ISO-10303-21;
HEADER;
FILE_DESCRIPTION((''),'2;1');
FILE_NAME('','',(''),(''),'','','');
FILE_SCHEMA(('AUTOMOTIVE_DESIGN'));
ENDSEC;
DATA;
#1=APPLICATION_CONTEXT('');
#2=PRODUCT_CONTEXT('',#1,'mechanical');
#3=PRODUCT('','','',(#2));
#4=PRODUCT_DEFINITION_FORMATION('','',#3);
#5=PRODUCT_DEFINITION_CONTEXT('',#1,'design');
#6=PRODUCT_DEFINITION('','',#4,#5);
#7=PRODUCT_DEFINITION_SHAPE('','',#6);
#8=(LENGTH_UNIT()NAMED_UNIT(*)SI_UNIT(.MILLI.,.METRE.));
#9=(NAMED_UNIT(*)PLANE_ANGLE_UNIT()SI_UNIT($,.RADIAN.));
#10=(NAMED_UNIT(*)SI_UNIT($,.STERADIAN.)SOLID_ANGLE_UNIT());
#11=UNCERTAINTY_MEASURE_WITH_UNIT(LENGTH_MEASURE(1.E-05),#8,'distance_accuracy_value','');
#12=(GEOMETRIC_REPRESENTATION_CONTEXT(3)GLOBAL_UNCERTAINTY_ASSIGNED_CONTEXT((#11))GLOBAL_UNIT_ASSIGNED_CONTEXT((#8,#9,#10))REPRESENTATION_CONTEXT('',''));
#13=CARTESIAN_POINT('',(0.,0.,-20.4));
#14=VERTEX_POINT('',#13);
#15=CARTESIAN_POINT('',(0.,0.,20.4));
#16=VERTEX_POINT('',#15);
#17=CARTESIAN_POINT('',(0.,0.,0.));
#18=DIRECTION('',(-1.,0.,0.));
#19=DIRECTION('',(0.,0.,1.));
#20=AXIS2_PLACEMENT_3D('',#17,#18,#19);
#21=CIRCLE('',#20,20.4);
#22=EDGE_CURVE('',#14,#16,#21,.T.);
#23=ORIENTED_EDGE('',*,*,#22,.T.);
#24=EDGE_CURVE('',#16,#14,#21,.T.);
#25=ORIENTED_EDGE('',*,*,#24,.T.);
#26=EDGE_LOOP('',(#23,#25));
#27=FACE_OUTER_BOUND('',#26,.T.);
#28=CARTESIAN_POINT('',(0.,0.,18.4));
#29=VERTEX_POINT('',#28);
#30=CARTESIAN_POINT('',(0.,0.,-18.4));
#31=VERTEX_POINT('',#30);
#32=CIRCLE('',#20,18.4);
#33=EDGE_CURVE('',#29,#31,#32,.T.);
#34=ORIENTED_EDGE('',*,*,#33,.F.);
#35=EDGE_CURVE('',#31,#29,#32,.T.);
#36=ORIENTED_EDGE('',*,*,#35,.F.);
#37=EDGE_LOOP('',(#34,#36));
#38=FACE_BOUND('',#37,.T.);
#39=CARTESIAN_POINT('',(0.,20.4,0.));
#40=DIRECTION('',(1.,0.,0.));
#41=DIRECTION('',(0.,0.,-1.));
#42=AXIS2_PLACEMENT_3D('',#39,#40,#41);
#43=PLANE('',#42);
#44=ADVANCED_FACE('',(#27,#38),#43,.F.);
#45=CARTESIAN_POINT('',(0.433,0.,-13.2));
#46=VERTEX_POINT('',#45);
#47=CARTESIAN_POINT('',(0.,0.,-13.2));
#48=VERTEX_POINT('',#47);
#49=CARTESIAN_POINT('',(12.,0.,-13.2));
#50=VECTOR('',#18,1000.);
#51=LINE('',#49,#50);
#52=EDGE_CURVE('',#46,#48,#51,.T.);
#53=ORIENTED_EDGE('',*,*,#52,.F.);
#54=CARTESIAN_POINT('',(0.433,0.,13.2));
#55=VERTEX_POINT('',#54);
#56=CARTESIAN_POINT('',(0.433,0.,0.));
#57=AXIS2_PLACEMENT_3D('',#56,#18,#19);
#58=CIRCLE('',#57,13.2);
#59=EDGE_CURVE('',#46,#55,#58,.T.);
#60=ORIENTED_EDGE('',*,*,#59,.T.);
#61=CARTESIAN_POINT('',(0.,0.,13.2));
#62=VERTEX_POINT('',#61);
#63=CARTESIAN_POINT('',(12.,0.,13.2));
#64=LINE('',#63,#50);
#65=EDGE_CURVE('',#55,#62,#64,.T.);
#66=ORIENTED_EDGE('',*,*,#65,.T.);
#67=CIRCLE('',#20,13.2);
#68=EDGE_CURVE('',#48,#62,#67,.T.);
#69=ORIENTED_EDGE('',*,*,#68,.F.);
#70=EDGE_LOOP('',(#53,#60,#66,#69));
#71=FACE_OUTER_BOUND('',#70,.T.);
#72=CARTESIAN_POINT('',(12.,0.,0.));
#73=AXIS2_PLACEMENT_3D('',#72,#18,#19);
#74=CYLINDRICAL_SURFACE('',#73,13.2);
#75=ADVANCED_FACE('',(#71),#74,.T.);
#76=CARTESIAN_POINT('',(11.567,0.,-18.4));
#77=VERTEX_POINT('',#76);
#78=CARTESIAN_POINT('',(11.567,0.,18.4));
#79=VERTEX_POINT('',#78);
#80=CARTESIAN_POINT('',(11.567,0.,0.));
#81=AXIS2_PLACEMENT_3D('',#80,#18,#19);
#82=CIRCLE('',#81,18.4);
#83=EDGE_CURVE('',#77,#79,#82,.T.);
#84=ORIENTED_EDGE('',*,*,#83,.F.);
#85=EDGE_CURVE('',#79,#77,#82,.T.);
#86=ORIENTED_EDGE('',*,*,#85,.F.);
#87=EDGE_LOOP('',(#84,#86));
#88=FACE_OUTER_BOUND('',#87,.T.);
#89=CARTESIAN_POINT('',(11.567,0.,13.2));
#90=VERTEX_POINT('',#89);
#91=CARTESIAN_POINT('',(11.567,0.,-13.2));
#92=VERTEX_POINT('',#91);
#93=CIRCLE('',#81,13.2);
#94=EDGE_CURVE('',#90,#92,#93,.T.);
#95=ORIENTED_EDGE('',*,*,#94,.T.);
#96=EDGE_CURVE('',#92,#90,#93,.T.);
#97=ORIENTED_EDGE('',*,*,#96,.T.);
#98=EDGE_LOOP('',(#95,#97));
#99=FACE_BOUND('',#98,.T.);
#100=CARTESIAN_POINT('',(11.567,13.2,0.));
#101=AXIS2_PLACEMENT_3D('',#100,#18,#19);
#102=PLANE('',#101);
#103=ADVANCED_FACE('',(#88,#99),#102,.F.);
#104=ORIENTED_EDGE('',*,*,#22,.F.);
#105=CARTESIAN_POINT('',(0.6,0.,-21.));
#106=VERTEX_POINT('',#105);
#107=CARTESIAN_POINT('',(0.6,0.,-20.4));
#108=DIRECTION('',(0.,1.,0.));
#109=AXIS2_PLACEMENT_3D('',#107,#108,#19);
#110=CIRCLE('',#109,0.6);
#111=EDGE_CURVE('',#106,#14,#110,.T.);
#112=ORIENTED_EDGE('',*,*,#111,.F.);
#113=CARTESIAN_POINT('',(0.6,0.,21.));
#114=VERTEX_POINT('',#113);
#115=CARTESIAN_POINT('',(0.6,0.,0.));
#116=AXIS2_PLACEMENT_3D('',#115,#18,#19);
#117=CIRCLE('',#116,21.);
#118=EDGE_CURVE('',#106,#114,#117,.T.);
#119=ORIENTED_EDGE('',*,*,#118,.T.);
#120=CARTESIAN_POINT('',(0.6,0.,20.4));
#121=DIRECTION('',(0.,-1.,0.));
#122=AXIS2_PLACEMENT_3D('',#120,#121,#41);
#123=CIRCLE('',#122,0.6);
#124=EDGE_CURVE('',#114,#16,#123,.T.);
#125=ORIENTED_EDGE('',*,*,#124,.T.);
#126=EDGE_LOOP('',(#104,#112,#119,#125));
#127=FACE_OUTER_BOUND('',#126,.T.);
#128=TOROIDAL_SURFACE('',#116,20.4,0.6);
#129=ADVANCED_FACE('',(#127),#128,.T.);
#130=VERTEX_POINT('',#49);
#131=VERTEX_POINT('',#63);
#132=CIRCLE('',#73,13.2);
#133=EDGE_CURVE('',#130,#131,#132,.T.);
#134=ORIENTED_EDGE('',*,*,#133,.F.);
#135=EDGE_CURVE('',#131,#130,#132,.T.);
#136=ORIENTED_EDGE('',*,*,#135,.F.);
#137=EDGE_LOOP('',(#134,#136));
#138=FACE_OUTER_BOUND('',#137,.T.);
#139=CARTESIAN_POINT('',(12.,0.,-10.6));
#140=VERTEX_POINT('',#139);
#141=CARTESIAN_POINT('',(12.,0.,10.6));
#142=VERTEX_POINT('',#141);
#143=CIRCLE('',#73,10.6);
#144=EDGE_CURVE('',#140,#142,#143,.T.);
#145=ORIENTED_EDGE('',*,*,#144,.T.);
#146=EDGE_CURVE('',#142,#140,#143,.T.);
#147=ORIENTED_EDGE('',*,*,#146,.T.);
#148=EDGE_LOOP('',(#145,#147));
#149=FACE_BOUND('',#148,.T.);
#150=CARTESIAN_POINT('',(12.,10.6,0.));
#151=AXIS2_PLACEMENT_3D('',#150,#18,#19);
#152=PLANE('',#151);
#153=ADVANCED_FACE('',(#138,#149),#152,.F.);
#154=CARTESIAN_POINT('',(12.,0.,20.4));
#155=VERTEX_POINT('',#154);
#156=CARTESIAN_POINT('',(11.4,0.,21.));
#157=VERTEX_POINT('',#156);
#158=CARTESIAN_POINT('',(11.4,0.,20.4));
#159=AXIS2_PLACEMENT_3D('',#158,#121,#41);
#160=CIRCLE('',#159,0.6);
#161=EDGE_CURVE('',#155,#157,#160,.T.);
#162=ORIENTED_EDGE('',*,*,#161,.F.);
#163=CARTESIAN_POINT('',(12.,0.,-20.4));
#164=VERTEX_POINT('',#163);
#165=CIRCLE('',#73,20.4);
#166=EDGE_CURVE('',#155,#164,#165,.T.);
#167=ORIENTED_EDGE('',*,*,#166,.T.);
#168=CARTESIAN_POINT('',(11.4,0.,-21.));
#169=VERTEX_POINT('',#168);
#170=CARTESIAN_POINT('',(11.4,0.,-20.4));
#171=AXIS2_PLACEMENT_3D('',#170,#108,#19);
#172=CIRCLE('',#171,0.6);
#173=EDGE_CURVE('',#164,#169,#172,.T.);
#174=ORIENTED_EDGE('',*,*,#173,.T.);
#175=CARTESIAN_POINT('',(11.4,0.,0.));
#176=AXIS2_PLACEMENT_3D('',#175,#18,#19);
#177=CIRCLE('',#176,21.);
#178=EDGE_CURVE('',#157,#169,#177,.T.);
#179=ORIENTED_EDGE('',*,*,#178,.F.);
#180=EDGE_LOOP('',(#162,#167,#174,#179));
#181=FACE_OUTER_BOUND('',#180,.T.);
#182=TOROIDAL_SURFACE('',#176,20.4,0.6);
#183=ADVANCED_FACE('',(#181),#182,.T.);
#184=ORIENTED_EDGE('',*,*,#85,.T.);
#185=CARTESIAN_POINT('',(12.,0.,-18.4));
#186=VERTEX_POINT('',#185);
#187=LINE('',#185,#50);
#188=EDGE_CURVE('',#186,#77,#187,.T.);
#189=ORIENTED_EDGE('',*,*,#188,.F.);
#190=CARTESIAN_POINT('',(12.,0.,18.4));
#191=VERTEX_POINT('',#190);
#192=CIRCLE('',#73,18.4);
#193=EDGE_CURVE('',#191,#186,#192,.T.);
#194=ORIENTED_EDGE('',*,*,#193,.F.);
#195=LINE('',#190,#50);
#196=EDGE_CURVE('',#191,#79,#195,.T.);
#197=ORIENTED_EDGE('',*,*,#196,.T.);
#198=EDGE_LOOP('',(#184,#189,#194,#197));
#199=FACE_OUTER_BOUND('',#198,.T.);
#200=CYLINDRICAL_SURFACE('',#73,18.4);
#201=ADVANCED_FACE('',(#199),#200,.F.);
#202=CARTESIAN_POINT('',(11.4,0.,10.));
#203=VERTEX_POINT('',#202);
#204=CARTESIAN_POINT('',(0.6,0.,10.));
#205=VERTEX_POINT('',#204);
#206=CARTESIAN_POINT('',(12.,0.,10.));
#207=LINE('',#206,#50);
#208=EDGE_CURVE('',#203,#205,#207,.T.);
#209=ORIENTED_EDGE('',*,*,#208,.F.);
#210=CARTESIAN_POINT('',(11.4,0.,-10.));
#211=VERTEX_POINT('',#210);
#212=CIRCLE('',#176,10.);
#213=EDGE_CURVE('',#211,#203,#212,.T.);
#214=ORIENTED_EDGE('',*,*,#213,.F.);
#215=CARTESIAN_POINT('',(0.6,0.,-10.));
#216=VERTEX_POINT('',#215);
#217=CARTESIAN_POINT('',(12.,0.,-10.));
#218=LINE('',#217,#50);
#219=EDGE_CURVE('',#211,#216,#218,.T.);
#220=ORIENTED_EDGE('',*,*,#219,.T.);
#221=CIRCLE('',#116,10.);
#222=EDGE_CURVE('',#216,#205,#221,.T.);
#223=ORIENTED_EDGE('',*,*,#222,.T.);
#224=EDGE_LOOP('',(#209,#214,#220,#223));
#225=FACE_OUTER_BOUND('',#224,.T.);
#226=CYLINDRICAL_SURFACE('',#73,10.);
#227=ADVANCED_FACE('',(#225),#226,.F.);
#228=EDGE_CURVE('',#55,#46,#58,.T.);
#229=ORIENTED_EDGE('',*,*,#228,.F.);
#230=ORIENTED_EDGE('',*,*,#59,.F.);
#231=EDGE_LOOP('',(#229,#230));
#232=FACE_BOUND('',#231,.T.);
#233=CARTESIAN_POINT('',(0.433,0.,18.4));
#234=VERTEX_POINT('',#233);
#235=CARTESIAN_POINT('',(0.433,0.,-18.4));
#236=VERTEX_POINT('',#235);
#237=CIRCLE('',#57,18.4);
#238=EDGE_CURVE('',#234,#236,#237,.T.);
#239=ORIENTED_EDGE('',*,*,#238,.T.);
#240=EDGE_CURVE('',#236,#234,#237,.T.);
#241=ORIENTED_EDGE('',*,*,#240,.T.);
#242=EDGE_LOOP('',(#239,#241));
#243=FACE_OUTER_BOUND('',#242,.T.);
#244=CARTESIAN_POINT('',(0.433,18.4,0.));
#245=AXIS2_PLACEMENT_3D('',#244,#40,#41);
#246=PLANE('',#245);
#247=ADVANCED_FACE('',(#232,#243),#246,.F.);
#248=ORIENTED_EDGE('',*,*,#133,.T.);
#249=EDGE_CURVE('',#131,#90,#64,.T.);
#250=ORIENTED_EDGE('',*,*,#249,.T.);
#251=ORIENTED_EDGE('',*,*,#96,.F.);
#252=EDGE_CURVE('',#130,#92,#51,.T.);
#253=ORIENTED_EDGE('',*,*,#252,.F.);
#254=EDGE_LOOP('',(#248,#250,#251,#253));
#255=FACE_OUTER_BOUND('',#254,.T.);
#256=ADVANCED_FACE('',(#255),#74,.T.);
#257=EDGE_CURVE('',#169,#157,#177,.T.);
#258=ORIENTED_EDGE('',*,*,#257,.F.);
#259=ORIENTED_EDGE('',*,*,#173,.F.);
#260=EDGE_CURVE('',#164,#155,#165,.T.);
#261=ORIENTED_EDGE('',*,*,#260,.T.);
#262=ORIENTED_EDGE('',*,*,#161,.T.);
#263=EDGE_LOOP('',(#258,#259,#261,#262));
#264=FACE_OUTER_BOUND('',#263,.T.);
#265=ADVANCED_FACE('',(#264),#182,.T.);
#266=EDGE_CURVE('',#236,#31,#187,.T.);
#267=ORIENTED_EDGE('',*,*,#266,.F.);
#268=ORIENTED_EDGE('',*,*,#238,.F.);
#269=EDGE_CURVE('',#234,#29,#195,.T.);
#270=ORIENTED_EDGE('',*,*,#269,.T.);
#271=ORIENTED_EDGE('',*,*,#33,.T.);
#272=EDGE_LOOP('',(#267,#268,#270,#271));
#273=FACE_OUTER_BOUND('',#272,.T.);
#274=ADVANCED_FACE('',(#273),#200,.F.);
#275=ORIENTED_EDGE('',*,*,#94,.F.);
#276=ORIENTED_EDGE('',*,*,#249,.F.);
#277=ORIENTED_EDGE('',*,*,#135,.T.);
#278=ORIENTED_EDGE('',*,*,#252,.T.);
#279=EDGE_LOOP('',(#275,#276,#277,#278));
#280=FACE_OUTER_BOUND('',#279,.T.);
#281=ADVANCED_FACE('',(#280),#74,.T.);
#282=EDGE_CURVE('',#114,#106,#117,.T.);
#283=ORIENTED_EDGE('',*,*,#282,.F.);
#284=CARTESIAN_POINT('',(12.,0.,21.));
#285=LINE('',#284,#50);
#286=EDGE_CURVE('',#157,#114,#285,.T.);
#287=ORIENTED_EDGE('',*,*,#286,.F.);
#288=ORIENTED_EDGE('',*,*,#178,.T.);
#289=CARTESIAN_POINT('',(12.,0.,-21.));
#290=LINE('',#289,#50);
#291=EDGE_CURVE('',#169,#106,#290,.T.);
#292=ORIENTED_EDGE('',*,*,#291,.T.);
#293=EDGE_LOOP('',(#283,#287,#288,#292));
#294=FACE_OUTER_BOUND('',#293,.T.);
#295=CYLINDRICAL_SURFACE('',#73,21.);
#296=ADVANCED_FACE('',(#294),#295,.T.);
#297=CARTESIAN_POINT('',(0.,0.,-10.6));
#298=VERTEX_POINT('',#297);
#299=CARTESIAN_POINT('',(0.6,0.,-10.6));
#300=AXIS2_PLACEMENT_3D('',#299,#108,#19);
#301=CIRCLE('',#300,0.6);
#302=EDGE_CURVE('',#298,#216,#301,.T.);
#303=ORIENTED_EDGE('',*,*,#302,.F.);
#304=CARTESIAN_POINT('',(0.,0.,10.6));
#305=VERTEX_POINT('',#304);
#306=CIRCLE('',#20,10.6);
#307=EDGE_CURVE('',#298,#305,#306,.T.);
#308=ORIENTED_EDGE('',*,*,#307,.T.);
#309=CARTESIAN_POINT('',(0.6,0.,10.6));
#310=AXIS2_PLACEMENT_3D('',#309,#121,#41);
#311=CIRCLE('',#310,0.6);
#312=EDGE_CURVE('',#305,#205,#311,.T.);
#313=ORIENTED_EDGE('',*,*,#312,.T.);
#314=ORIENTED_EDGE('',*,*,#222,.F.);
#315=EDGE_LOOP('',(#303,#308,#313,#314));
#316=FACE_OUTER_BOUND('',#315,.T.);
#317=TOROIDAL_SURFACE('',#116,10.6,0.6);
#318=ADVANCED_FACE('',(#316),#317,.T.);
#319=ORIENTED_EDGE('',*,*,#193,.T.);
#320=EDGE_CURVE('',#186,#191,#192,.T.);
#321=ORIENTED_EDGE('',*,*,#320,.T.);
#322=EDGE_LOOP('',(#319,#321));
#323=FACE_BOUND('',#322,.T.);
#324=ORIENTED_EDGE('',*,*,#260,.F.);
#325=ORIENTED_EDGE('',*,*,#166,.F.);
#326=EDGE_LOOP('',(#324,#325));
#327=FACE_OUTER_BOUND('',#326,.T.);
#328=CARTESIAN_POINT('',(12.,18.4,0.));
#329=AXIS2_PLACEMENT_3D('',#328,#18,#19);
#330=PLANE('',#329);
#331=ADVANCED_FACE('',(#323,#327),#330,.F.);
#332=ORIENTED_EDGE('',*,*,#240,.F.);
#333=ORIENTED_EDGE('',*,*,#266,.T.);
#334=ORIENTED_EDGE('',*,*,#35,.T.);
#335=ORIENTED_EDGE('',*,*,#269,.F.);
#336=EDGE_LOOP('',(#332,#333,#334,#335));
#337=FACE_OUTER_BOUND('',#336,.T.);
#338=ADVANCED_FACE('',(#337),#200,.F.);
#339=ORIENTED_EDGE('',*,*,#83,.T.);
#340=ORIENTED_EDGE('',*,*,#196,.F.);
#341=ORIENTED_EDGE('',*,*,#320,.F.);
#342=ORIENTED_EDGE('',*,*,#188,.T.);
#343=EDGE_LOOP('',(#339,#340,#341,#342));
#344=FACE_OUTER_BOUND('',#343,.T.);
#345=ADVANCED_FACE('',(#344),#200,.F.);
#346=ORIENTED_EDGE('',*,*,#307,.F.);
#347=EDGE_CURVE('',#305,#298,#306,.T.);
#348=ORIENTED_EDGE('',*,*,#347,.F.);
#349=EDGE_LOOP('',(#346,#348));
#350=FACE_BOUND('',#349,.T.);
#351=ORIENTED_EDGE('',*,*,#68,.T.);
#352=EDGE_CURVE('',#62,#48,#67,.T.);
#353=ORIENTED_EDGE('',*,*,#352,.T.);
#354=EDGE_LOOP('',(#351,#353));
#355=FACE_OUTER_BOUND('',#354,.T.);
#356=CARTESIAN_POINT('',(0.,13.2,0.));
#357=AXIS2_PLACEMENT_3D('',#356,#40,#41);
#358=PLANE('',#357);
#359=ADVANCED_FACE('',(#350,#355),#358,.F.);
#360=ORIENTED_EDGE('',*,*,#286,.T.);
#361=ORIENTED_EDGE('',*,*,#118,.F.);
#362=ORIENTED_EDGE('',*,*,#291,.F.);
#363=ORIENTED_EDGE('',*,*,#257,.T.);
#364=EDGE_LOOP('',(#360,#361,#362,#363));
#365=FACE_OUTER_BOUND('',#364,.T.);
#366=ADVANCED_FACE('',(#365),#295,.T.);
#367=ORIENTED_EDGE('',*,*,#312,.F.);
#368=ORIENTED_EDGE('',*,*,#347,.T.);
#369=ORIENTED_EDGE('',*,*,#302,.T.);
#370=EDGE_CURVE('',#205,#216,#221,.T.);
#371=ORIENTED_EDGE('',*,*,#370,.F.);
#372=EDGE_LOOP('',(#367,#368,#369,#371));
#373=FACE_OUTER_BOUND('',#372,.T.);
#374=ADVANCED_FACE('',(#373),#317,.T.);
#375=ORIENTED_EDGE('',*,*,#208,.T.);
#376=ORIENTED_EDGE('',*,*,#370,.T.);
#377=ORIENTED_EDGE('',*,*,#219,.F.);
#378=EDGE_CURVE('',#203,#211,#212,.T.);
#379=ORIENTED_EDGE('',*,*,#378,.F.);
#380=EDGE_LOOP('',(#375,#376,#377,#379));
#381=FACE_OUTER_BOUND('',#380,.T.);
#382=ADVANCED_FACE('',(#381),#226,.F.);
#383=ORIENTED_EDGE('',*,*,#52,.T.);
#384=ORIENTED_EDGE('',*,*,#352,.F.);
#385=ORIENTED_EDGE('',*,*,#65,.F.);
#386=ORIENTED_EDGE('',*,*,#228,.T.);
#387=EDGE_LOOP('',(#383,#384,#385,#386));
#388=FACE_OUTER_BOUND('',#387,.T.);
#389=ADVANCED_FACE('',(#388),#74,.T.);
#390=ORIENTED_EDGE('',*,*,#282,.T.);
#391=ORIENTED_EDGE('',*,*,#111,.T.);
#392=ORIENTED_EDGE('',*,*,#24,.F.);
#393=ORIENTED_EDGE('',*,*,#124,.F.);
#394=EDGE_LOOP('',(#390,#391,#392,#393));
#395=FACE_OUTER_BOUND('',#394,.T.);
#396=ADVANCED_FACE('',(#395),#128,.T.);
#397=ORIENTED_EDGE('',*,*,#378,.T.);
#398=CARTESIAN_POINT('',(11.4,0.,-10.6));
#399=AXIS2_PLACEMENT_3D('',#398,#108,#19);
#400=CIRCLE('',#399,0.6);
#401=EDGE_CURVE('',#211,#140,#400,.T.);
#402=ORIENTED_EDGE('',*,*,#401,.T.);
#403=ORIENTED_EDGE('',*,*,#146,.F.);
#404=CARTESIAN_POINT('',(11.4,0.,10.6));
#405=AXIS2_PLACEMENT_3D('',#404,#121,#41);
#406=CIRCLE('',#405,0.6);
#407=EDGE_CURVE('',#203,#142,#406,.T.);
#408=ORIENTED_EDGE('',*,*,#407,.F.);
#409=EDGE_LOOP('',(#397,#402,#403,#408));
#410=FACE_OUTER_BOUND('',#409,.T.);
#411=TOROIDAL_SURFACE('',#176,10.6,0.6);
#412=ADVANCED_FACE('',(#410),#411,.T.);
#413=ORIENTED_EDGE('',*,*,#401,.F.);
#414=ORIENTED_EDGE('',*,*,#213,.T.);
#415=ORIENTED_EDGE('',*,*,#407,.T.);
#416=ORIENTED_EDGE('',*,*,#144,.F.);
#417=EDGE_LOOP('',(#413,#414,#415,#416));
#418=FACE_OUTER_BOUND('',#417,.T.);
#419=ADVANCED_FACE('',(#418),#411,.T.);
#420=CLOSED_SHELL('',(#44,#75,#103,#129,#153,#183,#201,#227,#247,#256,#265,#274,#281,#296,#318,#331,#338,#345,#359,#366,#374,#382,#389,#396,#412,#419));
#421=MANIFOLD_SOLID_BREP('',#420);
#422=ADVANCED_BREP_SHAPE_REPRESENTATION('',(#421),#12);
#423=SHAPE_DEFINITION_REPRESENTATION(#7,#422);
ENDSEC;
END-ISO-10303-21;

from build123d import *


with BuildPart() as part:
    # 草图1 → 旋转1 (revolve)
    with BuildSketch(Plane.XY, mode=Mode.PRIVATE) as revolve_1_sk:
        with BuildLine():
            Line((0, 20.4), (0, 18.4))
            Line((0, 18.4), (0.433, 18.4))
            Line((0.433, 18.4), (0.433, 13.2))
            Line((0.433, 13.2), (0, 13.2))
            Line((0, 13.2), (0, 10.6))
            ThreePointArc((0, 10.6), (0.175735931, 10.175735931), (0.6, 10))
            Line((0.6, 10), (11.4, 10))
            ThreePointArc((11.4, 10), (11.824264069, 10.175735931), (12, 10.6))
            Line((12, 10.6), (12, 13.2))
            Line((12, 13.2), (11.567, 13.2))
            Line((11.567, 13.2), (11.567, 18.4))
            Line((11.567, 18.4), (12, 18.4))
            Line((12, 18.4), (12, 20.4))
            ThreePointArc((12, 20.4), (11.824264069, 20.824264069), (11.4, 21))
            Line((11.4, 21), (0.6, 21))
            ThreePointArc((0.6, 21), (0.175735931, 20.824264069), (0, 20.4))
        make_face()
    revolve(revolve_1_sk.sketch.rotate(Axis((12, 0, 0), (-1, 0, 0)), 270), axis=Axis((12, 0, 0), (-1, 0, 0)))


solid = part.part
